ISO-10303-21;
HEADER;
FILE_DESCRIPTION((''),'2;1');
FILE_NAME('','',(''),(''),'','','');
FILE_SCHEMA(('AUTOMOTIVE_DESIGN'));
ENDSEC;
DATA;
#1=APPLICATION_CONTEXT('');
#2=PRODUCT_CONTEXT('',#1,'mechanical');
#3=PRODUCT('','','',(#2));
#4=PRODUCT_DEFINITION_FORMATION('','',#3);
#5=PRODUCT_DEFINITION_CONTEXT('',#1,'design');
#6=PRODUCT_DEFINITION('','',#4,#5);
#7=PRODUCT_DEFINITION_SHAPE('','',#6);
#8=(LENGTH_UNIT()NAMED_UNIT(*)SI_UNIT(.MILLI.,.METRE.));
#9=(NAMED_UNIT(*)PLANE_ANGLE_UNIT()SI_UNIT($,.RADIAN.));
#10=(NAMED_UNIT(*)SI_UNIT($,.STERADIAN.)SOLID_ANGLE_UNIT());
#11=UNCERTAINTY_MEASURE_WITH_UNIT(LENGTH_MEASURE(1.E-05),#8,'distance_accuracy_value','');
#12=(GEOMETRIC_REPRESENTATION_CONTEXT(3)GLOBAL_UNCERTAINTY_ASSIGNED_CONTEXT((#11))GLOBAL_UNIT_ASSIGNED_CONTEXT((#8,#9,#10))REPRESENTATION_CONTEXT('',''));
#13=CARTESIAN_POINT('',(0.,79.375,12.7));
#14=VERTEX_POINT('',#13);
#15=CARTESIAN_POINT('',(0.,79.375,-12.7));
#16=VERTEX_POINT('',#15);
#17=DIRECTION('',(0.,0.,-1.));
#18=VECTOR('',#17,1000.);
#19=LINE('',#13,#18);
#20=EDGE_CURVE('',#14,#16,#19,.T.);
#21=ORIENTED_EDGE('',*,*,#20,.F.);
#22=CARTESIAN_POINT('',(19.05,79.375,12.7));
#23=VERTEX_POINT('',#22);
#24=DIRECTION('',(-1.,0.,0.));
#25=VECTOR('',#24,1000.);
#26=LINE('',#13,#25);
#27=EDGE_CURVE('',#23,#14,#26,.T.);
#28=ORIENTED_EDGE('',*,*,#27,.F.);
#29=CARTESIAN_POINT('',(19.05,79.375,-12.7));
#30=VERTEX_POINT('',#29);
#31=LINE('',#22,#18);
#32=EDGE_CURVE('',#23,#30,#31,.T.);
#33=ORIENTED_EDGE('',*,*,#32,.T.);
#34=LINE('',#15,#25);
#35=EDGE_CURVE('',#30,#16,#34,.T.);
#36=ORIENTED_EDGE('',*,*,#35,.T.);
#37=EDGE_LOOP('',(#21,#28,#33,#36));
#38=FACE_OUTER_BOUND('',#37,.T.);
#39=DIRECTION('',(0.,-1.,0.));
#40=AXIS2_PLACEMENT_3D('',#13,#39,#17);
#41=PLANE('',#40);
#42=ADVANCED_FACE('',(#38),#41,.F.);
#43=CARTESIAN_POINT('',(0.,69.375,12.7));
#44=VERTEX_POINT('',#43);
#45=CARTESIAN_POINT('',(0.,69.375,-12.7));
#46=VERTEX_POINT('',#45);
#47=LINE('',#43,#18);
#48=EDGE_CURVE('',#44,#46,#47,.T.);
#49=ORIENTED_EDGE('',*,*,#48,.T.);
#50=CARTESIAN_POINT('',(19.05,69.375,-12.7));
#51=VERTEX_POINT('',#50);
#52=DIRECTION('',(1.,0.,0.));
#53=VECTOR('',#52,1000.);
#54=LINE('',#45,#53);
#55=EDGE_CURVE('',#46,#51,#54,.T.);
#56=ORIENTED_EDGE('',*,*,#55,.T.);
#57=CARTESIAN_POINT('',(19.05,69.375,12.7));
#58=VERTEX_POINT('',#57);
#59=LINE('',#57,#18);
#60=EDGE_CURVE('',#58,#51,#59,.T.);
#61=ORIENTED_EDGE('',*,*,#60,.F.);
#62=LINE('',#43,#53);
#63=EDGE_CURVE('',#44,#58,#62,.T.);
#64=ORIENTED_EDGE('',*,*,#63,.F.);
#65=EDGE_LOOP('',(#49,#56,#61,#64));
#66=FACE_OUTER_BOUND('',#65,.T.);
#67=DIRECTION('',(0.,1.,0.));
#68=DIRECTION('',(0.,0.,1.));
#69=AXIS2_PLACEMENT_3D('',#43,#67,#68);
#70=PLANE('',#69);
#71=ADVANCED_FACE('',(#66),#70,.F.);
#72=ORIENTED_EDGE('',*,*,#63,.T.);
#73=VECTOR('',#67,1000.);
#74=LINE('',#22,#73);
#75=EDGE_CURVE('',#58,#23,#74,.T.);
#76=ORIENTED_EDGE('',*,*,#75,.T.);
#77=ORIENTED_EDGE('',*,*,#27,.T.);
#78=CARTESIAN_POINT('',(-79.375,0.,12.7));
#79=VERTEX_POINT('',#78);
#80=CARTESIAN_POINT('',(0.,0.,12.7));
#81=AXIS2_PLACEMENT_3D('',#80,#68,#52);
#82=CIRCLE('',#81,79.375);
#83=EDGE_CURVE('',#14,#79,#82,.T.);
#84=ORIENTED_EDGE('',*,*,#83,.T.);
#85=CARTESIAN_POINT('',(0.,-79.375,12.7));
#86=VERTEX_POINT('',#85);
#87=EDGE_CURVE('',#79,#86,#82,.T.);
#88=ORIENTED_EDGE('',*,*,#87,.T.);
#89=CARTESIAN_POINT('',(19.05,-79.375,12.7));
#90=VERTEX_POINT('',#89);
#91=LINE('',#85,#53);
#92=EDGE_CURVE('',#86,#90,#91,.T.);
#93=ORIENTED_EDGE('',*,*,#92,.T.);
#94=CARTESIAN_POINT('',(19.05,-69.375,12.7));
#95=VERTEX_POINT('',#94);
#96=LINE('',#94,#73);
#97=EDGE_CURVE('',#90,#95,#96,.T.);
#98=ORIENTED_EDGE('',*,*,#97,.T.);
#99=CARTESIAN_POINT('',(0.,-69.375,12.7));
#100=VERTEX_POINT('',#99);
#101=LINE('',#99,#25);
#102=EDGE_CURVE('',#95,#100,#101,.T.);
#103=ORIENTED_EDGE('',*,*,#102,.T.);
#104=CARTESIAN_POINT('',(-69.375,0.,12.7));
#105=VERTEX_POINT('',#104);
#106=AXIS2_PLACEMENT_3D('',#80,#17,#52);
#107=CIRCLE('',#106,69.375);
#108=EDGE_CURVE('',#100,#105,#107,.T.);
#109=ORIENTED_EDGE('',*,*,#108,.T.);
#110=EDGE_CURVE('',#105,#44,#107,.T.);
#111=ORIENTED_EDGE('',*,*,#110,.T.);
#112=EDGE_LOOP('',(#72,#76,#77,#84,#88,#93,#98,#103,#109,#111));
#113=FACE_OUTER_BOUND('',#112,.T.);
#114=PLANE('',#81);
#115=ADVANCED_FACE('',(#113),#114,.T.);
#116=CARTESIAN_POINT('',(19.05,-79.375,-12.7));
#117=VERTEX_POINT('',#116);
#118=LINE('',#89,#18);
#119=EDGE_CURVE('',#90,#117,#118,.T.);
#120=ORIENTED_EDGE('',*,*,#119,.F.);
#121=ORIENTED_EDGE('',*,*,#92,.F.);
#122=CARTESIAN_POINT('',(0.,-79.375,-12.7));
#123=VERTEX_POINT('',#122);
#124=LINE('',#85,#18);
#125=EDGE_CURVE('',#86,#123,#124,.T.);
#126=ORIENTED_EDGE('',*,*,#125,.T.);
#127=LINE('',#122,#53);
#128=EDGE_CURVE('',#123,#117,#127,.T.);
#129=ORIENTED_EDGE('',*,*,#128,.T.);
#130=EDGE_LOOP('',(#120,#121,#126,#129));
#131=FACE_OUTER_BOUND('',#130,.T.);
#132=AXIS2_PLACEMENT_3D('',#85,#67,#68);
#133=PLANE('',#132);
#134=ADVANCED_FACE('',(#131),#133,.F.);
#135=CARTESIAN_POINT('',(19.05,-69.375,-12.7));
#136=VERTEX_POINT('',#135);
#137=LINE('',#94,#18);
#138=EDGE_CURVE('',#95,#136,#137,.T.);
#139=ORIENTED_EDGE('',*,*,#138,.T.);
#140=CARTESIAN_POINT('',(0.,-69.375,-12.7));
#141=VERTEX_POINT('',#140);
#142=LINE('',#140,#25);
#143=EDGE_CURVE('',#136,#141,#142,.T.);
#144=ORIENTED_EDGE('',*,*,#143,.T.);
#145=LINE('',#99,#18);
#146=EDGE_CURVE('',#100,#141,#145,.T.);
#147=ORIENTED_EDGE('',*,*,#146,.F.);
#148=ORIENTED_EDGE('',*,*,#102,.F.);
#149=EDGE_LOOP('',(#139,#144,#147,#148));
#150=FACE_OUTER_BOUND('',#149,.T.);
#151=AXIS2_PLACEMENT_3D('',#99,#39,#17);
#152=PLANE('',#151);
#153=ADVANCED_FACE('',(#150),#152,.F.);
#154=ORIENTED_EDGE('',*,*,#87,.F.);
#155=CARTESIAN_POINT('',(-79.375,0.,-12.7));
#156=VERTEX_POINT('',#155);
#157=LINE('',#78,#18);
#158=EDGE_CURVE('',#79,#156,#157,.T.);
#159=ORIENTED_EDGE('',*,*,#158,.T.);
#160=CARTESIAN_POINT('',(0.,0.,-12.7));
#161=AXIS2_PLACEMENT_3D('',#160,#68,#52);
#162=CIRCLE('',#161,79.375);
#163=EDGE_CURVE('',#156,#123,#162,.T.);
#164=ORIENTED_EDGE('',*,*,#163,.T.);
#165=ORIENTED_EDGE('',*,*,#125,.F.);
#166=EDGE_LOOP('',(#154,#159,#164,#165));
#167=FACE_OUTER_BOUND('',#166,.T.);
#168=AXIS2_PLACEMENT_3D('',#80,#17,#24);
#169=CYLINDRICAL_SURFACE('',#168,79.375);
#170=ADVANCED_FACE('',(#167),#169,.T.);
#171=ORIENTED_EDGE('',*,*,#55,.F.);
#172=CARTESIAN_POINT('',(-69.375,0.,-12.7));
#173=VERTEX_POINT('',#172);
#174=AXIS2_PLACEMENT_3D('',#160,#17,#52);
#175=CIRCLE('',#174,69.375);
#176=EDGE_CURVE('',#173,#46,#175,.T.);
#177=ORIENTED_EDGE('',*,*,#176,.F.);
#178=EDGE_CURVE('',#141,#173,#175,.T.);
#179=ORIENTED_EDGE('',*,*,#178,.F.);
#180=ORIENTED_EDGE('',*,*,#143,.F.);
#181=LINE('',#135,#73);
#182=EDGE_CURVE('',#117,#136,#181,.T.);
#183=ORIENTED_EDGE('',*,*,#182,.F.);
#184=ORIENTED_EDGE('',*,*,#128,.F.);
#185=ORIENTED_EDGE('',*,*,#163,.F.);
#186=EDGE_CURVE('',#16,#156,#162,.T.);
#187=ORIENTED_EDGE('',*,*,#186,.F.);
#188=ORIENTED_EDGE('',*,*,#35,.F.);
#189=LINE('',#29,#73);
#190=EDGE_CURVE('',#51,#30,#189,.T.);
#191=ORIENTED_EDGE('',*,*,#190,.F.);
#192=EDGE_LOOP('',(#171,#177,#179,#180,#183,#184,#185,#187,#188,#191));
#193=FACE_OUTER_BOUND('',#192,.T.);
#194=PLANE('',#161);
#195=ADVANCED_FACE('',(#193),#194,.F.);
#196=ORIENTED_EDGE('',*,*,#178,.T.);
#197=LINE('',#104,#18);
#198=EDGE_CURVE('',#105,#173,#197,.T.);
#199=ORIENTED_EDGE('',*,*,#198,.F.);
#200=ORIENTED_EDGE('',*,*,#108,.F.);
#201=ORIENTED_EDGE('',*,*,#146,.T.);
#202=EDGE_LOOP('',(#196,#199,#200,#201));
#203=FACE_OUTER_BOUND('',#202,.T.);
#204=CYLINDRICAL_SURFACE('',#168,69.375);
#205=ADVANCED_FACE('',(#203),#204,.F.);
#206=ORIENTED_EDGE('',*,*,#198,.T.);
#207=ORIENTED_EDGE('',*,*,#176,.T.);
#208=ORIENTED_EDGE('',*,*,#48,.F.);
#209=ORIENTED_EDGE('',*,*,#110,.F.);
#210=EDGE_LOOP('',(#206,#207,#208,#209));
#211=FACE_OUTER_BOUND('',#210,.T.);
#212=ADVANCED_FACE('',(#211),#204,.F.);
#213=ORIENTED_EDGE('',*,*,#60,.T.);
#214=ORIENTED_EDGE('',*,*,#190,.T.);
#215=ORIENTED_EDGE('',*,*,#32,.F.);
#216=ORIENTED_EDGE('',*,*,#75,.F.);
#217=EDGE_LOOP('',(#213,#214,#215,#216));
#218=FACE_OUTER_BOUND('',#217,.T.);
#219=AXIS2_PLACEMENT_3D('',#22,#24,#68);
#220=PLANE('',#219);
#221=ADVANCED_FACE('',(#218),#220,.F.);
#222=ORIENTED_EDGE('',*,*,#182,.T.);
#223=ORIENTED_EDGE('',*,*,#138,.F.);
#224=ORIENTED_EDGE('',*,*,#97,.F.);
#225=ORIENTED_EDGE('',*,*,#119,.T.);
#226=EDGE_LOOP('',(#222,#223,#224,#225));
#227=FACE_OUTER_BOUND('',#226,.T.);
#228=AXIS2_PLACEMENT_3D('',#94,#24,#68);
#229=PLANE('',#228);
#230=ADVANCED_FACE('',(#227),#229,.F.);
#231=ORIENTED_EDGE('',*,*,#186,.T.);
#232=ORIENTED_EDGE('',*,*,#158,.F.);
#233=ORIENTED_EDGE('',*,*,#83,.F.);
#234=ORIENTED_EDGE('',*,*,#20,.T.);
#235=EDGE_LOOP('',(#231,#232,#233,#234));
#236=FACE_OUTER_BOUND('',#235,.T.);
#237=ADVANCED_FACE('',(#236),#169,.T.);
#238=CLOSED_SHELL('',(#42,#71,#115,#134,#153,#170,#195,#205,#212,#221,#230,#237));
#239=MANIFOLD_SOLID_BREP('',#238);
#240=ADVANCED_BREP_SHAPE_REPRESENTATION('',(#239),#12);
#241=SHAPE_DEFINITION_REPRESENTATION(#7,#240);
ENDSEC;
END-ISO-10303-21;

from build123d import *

# Parameters (mm, degrees)
BOSS_EXTRUDE1_DEPTH = 12.7


with BuildPart() as part:
    # Sketch1 → Boss-Extrude1 (new, symmetric)
    with BuildSketch(Plane.XY):
        with BuildLine():
            Line((0, 79.375), (19.05, 79.375))
            Line((19.05, 79.375), (19.05, 69.375))
            Line((19.05, 69.375), (0, 69.375))
            ThreePointArc((0, 69.375), (-69.375, 0), (0, -69.375))
            Line((0, -69.375), (19.05, -69.375))
            Line((19.05, -69.375), (19.05, -79.375))
            Line((19.05, -79.375), (0, -79.375))
            ThreePointArc((0, -79.375), (-79.375, 0), (0, 79.375))
        make_face()
    extrude(amount=BOSS_EXTRUDE1_DEPTH, both=True)


solid = part.part
